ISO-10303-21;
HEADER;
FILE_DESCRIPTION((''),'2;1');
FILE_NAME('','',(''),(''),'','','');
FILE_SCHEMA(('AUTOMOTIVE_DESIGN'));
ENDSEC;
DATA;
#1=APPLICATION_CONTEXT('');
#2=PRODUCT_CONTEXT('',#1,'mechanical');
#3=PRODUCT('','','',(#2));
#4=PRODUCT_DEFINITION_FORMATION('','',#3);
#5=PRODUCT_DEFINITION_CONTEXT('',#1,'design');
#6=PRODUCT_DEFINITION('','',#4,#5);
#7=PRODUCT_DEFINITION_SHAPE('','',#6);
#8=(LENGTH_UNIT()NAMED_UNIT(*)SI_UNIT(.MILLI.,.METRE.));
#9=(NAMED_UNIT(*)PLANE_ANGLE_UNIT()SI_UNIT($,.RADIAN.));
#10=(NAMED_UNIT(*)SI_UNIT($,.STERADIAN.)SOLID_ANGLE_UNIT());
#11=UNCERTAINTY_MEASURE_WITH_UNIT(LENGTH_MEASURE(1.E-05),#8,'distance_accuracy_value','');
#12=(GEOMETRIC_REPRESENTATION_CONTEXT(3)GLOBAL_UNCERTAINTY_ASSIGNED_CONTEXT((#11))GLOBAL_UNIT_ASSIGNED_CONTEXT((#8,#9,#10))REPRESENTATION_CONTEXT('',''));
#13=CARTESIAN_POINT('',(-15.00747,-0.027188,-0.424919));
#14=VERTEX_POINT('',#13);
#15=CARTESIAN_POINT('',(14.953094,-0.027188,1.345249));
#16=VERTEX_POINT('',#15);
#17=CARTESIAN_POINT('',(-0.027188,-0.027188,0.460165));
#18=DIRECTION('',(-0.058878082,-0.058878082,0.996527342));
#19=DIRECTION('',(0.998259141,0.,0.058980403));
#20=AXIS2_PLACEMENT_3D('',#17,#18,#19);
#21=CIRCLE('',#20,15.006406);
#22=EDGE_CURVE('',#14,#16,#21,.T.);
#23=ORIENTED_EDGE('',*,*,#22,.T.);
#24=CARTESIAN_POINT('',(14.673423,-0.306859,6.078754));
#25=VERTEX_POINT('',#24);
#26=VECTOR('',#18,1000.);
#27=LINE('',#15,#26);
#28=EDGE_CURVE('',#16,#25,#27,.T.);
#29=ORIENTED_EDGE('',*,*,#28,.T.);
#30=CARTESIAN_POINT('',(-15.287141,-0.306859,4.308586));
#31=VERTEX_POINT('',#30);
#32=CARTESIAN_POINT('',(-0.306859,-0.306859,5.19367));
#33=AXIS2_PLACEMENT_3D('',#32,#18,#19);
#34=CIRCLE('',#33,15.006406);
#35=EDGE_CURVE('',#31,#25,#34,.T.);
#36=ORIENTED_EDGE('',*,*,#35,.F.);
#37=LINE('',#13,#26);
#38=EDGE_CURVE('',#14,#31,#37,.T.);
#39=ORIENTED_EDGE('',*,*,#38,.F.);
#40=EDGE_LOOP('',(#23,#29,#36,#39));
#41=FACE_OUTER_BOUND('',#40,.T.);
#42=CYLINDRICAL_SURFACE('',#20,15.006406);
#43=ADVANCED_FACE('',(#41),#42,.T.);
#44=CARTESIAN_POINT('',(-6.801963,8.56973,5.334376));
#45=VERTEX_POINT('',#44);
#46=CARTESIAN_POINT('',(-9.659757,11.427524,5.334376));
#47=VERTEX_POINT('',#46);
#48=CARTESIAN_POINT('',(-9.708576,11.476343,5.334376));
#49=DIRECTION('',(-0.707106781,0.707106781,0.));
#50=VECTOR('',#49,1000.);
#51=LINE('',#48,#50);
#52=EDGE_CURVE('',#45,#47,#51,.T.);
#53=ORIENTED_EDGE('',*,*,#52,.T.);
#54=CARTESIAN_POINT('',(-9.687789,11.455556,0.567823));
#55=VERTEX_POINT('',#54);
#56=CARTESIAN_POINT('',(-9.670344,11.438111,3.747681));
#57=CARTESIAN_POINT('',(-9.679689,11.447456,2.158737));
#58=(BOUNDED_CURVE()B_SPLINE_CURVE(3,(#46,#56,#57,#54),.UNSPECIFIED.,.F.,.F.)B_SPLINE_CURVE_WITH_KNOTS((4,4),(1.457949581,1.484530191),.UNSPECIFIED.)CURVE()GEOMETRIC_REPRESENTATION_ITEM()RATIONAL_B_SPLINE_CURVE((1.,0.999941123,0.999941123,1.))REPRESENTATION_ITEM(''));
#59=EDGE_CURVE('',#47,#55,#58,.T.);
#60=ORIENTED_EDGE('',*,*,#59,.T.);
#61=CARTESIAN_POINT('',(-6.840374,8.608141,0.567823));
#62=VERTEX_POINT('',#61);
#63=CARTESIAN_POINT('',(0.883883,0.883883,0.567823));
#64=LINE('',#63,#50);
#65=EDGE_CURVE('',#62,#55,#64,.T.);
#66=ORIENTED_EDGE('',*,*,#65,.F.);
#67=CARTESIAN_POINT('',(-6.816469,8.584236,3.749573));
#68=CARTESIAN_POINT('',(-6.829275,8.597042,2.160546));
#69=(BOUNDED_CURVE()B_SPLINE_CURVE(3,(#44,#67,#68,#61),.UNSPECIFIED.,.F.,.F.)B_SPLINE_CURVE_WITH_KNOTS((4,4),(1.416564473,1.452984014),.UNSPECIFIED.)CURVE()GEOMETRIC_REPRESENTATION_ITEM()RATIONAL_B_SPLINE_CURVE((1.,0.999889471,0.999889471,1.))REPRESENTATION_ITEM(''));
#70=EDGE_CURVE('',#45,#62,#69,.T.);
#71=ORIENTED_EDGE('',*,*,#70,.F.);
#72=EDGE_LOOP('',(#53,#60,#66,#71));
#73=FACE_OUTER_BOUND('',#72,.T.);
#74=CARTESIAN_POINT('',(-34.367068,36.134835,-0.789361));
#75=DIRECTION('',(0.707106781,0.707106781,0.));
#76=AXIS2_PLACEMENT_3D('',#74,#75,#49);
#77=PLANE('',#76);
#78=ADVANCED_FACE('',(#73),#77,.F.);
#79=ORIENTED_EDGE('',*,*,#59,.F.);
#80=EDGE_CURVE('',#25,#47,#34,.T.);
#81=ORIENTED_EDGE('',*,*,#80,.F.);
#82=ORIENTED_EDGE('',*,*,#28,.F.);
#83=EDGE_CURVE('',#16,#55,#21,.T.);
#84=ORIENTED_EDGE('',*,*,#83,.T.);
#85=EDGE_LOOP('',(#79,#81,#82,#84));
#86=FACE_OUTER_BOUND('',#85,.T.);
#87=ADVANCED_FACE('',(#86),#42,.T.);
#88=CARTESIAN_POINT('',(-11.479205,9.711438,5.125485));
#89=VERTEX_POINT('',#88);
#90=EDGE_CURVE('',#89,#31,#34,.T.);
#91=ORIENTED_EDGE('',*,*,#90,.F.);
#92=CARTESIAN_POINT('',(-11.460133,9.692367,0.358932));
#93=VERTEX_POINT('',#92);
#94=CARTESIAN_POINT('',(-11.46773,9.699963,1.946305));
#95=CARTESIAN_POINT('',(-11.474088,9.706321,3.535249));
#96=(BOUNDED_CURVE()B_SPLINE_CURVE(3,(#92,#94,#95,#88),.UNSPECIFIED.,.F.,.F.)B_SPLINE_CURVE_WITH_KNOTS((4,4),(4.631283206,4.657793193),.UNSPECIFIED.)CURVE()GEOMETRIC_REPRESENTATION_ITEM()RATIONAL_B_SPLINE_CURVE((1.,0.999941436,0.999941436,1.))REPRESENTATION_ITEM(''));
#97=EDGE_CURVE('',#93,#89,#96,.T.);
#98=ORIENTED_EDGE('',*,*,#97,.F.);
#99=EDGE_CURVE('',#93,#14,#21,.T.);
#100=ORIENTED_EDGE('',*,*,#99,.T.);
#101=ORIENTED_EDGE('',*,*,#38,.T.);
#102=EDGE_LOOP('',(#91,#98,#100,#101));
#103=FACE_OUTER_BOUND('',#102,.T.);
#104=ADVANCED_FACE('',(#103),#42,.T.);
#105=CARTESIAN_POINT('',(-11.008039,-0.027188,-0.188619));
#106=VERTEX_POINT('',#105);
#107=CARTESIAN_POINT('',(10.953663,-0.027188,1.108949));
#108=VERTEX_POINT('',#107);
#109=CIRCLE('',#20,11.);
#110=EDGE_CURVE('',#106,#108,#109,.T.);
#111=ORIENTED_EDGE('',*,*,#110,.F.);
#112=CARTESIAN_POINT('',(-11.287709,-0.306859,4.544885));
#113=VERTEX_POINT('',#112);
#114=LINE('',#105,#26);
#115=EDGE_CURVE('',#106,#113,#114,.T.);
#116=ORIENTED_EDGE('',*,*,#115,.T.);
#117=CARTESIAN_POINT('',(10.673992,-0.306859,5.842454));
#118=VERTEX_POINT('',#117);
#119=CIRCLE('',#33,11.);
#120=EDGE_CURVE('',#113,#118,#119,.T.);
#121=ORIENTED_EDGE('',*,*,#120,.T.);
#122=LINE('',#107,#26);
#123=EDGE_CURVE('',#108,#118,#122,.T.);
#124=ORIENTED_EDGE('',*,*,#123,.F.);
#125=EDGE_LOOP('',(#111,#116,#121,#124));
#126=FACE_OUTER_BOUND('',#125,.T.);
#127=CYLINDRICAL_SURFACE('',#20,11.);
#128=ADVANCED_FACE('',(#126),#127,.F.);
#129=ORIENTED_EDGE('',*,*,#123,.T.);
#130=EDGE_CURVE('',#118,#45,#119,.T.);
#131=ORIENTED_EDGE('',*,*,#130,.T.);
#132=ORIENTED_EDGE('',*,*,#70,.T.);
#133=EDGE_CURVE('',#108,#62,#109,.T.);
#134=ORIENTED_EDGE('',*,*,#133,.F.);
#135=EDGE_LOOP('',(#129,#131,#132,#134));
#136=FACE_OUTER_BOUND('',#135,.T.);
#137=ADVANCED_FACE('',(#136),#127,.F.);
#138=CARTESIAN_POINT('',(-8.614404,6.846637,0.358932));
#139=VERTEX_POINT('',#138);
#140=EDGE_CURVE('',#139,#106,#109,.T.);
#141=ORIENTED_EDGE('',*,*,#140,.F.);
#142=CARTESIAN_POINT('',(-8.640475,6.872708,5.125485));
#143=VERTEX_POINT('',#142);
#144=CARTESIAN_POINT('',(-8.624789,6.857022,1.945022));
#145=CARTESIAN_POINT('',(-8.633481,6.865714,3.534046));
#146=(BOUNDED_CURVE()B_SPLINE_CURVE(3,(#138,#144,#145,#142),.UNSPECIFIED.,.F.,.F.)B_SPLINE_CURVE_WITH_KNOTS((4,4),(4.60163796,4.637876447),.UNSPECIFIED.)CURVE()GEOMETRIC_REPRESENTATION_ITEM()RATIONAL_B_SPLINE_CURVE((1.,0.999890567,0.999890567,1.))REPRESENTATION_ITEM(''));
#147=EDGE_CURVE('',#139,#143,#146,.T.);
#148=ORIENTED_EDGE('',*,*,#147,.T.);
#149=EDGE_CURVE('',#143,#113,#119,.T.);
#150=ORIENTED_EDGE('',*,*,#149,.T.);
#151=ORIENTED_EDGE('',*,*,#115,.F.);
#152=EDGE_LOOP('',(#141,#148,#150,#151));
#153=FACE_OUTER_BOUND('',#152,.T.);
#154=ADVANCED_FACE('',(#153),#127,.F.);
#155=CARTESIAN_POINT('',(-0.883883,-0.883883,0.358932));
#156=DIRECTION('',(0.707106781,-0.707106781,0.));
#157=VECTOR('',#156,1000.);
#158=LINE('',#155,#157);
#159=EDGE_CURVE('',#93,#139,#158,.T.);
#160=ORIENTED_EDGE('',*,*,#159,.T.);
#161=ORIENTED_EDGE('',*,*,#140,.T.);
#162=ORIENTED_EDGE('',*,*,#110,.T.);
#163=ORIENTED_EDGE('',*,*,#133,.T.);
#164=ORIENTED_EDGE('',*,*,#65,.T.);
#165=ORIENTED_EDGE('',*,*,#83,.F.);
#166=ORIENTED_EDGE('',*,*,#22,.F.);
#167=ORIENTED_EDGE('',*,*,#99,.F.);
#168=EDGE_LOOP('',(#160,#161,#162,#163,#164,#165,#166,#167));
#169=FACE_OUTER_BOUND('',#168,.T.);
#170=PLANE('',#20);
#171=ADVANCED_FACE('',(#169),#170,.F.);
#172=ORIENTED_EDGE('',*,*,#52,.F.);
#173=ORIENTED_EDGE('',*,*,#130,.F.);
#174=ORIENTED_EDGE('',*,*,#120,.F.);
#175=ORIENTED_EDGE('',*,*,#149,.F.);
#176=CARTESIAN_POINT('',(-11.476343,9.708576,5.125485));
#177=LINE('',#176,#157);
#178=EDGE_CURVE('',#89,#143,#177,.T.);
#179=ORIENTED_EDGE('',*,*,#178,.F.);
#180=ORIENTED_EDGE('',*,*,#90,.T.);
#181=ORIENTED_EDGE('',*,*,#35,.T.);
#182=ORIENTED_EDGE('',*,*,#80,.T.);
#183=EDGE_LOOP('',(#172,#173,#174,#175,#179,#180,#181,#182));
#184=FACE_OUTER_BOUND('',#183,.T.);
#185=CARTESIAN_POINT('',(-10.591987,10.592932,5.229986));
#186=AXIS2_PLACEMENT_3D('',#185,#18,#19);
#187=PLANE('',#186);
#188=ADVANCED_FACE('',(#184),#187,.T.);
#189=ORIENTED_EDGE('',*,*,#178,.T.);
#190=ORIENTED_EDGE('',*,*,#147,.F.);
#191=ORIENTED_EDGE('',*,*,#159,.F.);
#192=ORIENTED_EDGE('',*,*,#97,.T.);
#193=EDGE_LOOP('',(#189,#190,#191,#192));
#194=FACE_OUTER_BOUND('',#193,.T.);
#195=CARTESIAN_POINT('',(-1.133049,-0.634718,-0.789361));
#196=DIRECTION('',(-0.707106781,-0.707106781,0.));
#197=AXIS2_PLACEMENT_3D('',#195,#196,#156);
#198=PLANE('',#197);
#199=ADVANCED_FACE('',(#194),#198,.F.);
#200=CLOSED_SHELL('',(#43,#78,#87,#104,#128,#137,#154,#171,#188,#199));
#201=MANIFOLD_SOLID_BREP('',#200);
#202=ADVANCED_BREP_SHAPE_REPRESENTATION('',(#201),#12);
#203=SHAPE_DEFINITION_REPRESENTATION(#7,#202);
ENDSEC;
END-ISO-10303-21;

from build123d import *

# Parameters (mm, degrees)
BASE_EXTRUDE_DEPTH      = 0.001
BASE_EXTRUDE_DEPTH_BACK = 0.001
SKETCH6_W               = 4.71
SKETCH6_H               = 4.96
SKETCH8_R               = 15.00640628
SKETCH8_R_2             = 11
BOSS_EXTRUDE1_DEPTH     = 4.75
CUT_EXTRUDE1_DEPTH      = 23.559115412
CUT_EXTRUDE1_DEPTH_BACK = 23.559115412


with BuildPart() as part:
    # Sketch6 → Base-Extrude (new, two sides: drawn at the far end of the back side and taken through both)
    with BuildSketch(Plane(origin=(-7.071067812, 7.071067812, 5.25), x_dir=(0.05887808228355755, 0.05887808228355607, -0.9965273417489464), z_dir=(0.7046512409884902, 0.7046512409884782, 0.0832661824919251)).offset(-BASE_EXTRUDE_DEPTH_BACK)):
        with Locations((2.375, 2.5)):
            Rectangle(SKETCH6_W, SKETCH6_H)
    extrude(amount=BASE_EXTRUDE_DEPTH + BASE_EXTRUDE_DEPTH_BACK)

    # Sketch8 → Boss-Extrude1 (add)
    with BuildSketch(Plane(origin=(-0.306858937, -0.306858937, 5.193669853), x_dir=(0.9982651276202565, -0.00379884698167672, 0.05875630807770913), z_dir=(-0.05887808228355744, -0.05887808228355621, 0.9965273417489464))):
        with Locations(Location((0, 0, 0), (0, 0, 0.218036679))):
            Circle(SKETCH8_R)
        with Locations(Location((0, 0, 0), (0, 0, 0.218036679))):
            Circle(SKETCH8_R_2, mode=Mode.SUBTRACT)
    extrude(amount=-BOSS_EXTRUDE1_DEPTH)

    # Sketch9 → Cut-Extrude1 (cut, two sides: drawn at the far end of the back side and taken through both)
    with BuildSketch(Plane.XY.offset(-CUT_EXTRUDE1_DEPTH_BACK)):
        Polygon((-34.36706796, 36.134834913), (0.634717709, 1.133049244), (-1.133049244, -0.634717709), (-37.902601866, 36.134834913), align=None)
    extrude(amount=CUT_EXTRUDE1_DEPTH + CUT_EXTRUDE1_DEPTH_BACK, mode=Mode.SUBTRACT)


solid = part.part
